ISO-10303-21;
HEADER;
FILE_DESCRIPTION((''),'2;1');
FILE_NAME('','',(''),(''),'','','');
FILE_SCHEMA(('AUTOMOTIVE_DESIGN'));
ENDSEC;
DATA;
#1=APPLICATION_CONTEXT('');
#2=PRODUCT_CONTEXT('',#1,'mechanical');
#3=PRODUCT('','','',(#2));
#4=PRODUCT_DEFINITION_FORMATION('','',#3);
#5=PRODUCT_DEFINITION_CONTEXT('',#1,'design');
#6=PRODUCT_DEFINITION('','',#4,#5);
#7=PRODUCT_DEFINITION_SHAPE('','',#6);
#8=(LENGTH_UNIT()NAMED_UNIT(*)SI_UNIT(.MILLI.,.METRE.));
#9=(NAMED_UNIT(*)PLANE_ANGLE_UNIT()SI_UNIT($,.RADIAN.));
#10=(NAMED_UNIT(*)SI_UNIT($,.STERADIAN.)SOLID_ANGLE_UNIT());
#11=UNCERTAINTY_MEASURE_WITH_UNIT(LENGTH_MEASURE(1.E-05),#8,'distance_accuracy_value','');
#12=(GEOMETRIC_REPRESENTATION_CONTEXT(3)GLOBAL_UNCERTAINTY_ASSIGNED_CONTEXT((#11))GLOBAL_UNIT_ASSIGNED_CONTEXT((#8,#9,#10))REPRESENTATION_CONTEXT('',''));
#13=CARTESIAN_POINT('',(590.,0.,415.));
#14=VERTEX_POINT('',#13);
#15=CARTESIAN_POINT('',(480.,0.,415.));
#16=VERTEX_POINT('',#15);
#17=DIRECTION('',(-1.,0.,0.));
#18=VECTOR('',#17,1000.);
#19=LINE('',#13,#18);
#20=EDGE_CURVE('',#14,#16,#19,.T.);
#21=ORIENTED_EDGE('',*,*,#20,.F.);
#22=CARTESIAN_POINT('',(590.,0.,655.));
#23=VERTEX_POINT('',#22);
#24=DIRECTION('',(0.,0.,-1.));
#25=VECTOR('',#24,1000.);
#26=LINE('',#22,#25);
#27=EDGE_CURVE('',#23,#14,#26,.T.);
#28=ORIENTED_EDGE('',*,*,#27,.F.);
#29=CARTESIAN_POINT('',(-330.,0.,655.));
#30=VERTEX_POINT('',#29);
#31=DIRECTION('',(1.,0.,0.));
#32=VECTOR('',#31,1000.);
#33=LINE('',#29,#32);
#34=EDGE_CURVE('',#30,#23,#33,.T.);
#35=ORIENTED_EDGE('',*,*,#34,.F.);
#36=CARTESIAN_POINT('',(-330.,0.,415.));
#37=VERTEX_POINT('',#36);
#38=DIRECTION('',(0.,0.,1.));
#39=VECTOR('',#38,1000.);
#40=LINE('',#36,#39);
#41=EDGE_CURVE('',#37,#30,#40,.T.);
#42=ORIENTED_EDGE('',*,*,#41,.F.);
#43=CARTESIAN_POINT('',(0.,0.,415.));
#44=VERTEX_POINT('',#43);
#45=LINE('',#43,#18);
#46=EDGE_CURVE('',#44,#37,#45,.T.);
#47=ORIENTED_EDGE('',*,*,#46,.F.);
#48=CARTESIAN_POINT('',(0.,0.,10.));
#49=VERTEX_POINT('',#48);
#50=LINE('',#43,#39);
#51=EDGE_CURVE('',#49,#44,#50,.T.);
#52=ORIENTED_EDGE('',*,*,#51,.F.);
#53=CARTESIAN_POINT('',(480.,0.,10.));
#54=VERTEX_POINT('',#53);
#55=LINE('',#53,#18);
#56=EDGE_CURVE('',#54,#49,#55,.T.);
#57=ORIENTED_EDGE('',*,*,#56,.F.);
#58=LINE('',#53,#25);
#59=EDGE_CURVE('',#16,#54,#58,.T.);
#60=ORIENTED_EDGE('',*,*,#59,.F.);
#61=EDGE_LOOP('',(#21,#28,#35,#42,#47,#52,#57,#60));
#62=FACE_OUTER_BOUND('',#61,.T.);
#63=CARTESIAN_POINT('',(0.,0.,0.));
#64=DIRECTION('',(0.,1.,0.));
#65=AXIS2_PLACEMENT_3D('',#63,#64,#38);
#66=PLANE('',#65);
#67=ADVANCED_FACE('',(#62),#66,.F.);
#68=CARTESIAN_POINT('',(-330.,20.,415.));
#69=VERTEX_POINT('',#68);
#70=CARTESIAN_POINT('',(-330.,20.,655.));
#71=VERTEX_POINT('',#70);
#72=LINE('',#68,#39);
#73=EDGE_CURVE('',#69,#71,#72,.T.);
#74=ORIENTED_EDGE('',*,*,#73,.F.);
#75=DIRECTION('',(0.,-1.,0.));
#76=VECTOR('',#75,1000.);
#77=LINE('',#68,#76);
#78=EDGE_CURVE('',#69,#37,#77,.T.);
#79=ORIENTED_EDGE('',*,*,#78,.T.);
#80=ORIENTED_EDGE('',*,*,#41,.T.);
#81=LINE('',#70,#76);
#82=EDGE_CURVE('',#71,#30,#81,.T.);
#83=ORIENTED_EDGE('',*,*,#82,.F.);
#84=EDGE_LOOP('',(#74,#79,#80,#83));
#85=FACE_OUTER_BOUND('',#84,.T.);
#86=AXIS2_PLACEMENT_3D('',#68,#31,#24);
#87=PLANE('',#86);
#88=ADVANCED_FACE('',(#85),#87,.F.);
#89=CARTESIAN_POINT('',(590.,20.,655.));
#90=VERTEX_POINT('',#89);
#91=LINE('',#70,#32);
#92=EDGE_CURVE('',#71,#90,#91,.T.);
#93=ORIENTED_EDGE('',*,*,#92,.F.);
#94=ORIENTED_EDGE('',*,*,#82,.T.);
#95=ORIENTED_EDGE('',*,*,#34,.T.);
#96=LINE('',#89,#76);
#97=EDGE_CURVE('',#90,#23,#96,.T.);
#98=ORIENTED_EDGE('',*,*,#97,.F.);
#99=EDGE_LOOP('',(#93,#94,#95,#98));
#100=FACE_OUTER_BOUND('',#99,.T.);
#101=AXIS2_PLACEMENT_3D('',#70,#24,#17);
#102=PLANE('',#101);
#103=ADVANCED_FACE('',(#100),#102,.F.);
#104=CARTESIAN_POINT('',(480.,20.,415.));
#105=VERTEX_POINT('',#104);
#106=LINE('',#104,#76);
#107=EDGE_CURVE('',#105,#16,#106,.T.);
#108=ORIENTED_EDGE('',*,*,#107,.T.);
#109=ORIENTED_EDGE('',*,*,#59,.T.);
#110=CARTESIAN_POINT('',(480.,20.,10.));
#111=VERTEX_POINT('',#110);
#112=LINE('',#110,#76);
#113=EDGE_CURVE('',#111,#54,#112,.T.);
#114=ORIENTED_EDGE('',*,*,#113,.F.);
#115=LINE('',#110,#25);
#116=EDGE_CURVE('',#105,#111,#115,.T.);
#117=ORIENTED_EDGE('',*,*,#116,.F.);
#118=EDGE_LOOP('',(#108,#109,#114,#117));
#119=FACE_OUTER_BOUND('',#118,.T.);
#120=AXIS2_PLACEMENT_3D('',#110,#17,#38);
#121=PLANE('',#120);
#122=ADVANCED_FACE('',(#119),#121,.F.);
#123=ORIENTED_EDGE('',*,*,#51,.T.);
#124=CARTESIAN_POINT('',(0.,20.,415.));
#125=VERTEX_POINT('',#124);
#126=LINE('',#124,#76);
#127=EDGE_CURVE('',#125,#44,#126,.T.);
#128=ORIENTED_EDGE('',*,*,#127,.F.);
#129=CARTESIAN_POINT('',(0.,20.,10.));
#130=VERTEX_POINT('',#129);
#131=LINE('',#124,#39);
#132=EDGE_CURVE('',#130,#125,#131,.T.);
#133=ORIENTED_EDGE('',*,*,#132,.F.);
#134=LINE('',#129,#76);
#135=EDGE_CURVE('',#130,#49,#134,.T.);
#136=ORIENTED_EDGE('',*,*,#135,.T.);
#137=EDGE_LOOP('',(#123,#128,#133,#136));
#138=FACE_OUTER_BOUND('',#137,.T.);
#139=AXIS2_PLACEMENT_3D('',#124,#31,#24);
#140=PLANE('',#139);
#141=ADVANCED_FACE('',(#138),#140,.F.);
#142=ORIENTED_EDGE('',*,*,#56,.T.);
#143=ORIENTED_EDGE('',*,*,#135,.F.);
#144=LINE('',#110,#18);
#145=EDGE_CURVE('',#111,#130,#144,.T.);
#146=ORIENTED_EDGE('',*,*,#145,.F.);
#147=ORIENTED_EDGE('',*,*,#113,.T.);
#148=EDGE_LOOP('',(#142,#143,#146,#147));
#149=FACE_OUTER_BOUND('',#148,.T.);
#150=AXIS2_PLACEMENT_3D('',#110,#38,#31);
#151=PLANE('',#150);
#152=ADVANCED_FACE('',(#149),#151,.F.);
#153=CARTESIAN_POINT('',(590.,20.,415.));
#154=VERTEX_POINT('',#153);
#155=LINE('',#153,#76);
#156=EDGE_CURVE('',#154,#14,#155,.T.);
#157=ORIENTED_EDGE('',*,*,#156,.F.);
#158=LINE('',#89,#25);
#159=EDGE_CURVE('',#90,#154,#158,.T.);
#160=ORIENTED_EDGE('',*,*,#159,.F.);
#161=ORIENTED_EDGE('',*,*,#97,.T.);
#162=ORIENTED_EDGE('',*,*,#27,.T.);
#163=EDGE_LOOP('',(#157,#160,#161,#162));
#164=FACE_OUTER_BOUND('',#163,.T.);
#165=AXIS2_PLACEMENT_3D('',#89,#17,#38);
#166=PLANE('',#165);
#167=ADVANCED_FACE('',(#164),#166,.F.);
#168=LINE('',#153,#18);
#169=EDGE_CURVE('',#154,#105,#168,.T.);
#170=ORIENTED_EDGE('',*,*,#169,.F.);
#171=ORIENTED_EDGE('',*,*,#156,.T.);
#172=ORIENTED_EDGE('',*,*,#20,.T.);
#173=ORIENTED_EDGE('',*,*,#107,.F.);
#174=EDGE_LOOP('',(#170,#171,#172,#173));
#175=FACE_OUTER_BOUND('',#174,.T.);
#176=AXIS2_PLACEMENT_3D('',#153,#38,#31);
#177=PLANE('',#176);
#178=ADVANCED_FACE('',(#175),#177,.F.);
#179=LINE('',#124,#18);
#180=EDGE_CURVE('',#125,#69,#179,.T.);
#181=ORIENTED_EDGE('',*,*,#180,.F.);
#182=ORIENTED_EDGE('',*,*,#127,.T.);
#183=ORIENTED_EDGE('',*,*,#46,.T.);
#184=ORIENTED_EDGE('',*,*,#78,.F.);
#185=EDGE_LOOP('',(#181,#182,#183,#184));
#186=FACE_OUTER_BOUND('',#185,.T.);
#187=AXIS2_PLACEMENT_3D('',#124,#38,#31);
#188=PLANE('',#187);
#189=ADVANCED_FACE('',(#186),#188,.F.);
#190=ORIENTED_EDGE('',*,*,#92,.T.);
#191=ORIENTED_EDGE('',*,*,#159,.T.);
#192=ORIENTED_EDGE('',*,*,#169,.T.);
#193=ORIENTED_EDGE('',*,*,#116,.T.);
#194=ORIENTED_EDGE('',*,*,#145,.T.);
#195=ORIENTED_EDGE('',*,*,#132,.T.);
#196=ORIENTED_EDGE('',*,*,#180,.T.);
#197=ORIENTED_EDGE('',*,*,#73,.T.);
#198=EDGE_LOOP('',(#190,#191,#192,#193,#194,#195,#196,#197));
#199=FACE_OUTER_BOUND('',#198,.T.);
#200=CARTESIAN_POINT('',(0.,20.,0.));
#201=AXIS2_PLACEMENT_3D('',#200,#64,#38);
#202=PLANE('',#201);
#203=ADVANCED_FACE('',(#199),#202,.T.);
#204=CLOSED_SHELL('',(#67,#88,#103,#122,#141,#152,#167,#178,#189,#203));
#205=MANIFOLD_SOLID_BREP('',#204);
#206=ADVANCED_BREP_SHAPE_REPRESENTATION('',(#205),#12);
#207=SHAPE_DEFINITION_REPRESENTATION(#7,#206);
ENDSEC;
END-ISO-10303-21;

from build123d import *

# Parameters (mm, degrees)
BOSS_EXTRUDE1_DEPTH = 20


with BuildPart() as part:
    # Sketch1 → Boss-Extrude1 (new body)
    with BuildSketch(Plane(origin=(0, 0, 0), x_dir=(1, 0, 0), z_dir=(0, 1, 0))):
        Polygon((-330, -655), (590, -655), (590, -415), (480, -415), (480, -10), (0, -10), (0, -415), (-330, -415), align=None)
    extrude(amount=BOSS_EXTRUDE1_DEPTH)


solid = part.part
